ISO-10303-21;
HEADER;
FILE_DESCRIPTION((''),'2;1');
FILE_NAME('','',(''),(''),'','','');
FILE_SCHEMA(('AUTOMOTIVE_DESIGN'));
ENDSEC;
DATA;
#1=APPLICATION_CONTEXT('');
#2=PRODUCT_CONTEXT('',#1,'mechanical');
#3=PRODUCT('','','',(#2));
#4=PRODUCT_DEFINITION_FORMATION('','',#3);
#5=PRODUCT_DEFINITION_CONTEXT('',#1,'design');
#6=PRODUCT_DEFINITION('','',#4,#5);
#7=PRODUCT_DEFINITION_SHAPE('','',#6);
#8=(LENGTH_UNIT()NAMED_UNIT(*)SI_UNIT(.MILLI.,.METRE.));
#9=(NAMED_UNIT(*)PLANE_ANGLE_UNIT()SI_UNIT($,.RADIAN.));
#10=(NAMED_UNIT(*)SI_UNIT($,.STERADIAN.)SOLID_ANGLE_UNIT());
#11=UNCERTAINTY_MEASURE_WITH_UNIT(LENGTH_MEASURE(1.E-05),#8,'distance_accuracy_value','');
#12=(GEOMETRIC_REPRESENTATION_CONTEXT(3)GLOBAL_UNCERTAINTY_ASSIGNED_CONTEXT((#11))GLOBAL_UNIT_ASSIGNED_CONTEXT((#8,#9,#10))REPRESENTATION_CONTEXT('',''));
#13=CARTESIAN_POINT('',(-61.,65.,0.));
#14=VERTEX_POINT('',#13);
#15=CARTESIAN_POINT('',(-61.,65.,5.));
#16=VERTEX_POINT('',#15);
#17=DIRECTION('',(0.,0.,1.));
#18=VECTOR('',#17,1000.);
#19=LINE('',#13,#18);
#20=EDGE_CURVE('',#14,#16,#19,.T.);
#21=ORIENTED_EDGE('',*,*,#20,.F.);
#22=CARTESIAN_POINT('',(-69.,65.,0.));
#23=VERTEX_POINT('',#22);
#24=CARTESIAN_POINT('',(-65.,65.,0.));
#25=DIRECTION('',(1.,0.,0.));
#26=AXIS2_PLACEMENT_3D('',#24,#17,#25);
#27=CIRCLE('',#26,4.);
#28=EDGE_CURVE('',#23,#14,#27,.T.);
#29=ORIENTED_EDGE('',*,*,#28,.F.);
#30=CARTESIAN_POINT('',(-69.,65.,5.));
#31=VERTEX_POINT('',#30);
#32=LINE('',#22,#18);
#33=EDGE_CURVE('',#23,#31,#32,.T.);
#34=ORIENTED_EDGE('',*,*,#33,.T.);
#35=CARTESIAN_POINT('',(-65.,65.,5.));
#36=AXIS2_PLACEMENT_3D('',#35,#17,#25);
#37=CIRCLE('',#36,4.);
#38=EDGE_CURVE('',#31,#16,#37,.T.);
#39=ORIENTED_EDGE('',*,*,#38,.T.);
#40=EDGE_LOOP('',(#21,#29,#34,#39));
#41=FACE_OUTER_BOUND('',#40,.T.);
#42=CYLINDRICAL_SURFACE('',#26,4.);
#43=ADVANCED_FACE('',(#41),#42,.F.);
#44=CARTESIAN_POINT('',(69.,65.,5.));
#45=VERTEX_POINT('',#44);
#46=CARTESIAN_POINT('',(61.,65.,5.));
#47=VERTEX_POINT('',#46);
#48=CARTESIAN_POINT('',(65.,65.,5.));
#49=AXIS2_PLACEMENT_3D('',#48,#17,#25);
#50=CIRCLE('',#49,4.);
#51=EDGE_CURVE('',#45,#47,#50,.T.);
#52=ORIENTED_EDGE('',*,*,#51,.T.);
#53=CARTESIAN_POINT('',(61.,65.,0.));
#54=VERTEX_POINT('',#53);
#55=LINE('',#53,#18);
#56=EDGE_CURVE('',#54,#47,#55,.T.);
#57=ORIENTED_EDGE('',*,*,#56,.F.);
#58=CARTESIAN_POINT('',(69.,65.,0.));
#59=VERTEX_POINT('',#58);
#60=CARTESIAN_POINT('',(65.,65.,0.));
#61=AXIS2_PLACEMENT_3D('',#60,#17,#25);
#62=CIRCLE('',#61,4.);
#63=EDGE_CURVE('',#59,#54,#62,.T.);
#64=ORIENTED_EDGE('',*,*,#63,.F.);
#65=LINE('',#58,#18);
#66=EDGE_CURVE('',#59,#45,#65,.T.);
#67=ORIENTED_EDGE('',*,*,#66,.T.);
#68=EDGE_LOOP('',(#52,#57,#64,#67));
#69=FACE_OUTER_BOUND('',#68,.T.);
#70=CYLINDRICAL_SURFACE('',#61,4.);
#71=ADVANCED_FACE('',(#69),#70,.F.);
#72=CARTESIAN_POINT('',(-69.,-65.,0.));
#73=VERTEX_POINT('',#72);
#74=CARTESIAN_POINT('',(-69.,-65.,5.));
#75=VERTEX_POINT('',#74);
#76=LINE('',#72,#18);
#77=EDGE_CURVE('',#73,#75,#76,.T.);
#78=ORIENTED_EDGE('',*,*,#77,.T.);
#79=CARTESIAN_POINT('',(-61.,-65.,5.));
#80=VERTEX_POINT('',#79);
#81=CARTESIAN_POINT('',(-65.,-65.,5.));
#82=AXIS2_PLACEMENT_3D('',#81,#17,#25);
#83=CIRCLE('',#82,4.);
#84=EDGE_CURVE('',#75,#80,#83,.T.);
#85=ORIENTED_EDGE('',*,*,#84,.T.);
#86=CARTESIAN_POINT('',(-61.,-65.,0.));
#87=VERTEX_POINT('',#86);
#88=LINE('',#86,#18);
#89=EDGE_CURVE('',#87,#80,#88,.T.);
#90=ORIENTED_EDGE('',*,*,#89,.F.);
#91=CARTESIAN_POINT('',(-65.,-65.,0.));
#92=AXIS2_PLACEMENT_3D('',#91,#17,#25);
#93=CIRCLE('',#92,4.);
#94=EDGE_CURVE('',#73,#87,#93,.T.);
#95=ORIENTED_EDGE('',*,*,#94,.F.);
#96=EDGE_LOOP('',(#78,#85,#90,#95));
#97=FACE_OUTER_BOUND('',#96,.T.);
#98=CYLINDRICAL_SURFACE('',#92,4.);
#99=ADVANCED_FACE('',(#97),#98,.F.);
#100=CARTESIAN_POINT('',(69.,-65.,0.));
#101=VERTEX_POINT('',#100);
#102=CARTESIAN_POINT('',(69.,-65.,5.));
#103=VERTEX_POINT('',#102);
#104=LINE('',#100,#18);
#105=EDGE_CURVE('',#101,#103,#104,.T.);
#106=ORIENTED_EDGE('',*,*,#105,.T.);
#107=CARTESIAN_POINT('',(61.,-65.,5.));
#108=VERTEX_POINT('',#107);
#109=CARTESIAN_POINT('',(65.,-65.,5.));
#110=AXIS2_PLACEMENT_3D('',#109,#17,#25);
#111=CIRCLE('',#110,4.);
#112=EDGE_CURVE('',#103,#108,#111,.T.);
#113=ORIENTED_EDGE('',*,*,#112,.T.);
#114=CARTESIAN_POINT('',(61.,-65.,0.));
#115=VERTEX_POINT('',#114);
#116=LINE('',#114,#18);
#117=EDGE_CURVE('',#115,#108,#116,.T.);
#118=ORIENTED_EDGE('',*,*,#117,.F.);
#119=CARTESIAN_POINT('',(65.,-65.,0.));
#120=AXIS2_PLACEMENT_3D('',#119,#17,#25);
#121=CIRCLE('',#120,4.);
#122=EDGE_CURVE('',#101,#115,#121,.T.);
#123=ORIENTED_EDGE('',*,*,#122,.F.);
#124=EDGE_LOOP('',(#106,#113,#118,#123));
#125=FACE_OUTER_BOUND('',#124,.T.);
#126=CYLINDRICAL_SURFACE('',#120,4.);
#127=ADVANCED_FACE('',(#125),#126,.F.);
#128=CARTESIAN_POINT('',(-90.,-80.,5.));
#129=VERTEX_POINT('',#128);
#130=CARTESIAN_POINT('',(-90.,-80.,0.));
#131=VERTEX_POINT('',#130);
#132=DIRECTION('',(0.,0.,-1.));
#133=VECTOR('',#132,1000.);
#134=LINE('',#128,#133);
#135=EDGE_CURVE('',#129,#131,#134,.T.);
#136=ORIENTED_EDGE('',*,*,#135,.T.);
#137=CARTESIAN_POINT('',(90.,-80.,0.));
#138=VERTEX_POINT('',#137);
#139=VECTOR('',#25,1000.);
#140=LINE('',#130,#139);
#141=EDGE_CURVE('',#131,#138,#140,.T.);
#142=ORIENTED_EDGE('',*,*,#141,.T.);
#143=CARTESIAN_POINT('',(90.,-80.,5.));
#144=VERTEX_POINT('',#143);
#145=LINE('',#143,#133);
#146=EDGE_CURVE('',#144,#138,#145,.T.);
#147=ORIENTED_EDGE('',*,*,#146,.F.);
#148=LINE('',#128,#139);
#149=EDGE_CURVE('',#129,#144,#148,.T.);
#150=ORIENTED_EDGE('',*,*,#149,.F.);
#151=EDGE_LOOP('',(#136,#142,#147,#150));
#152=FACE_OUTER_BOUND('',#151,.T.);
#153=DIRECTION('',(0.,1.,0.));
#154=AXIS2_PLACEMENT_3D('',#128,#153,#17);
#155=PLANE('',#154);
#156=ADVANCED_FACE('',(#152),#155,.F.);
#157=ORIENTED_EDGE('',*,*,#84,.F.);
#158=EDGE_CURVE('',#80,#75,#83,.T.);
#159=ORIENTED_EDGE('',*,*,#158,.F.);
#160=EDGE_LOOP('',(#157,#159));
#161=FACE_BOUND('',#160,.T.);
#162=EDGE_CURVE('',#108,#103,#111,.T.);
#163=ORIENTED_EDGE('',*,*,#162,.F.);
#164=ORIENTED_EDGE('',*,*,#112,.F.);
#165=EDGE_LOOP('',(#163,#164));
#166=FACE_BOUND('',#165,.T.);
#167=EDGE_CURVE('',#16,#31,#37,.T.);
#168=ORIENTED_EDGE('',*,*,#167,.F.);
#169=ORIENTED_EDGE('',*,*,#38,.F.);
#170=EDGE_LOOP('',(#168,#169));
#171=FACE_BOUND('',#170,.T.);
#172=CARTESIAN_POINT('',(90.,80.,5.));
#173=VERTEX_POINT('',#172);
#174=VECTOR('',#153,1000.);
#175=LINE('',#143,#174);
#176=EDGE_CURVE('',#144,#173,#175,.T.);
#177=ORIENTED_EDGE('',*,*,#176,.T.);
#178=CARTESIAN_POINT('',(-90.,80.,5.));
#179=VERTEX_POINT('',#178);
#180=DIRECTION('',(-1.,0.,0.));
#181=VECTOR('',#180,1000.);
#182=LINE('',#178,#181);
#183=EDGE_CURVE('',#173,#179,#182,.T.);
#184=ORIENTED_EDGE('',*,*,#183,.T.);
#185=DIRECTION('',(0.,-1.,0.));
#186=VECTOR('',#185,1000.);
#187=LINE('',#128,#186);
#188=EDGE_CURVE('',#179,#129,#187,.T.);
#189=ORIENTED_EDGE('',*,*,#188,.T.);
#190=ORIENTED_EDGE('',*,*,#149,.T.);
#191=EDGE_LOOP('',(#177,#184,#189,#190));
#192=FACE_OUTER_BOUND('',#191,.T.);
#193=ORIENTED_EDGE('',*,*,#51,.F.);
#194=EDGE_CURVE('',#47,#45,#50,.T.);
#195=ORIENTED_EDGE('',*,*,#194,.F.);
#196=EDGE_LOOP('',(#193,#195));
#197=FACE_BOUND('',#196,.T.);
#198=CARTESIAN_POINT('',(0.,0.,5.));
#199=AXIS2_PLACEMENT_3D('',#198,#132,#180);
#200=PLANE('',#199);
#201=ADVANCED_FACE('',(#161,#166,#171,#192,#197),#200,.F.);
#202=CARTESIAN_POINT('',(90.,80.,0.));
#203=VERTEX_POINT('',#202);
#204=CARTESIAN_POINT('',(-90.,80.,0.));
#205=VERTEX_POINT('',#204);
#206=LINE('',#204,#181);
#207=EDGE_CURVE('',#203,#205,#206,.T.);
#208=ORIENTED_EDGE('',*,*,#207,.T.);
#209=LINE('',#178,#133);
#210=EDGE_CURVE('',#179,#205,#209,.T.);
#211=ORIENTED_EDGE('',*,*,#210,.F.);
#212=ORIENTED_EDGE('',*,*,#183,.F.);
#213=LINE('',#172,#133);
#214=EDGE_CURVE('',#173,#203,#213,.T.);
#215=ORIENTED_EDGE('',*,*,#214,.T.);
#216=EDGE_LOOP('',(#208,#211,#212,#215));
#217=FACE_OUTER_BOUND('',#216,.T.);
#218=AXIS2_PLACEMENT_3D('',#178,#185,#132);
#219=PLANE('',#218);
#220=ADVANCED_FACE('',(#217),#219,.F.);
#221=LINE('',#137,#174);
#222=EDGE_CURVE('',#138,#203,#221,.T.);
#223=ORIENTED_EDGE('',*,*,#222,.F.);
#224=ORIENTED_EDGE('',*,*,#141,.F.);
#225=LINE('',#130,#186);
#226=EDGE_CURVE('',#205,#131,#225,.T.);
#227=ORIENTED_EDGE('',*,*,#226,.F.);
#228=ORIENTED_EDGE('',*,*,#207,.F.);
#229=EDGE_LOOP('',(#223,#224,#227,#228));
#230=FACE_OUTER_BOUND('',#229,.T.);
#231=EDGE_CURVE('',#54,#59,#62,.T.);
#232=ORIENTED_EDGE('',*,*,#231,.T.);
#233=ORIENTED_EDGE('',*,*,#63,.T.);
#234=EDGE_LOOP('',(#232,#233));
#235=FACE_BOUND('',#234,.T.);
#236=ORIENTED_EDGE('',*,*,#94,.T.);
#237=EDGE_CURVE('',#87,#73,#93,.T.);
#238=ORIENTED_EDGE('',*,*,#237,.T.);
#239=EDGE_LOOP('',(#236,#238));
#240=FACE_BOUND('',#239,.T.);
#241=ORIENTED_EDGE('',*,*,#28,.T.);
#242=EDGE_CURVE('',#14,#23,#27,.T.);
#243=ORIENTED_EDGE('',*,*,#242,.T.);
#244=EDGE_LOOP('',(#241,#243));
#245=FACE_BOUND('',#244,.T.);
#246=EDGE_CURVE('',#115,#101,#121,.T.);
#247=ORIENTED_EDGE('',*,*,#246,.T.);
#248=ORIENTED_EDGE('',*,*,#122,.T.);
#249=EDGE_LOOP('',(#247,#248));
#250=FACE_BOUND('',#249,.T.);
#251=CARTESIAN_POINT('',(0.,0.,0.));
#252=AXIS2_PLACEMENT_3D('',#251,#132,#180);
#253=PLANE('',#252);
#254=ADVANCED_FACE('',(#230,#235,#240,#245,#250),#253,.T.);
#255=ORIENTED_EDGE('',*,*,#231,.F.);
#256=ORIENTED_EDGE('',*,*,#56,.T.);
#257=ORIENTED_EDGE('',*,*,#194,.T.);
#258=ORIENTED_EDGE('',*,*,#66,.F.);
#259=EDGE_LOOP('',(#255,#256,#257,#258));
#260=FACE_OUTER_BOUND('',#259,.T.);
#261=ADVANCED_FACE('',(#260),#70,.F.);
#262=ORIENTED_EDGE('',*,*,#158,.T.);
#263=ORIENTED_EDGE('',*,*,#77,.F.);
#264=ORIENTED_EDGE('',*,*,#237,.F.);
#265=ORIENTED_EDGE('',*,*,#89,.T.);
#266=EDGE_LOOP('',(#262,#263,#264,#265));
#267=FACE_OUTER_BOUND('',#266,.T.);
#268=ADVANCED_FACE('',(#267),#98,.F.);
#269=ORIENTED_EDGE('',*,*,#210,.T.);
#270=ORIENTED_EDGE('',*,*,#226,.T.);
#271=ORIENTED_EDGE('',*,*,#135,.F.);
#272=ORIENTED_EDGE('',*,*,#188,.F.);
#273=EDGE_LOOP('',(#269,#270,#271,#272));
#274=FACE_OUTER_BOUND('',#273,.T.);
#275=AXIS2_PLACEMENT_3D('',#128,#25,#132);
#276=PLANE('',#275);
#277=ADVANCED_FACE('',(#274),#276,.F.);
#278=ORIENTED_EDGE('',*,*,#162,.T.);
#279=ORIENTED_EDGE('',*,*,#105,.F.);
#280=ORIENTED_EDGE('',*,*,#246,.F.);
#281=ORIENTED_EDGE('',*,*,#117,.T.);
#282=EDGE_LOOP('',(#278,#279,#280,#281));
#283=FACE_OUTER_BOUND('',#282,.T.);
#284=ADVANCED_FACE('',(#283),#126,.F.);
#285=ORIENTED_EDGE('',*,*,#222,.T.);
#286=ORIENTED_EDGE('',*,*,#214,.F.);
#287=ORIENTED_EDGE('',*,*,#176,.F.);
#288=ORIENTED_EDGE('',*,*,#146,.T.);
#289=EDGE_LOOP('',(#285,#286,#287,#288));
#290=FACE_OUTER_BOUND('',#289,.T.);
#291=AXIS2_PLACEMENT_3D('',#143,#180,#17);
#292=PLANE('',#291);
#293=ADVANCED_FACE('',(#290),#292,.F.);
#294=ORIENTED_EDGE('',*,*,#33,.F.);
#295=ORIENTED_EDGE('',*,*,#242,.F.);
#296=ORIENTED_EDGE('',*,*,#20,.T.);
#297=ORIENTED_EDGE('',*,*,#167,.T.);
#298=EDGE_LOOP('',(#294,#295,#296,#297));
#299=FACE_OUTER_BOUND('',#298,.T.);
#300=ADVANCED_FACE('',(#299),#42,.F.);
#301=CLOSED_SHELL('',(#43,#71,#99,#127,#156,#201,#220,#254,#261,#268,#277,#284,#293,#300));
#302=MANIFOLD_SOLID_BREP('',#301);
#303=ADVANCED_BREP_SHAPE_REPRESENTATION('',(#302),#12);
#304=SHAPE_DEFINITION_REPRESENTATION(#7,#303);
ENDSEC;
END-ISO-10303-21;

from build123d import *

# Parameters (mm, degrees)
SKETCH_1_W          = 180
SKETCH_1_H          = 160
EXTRUDE_1_DEPTH     = 5
SKETCH_2_R          = 4
CUT_EXTRUDE_1_DEPTH = 121.519707932


with BuildPart() as part:
    # 草图1 → 凸台-拉伸1 (new body)
    with BuildSketch(Plane.XY):
        Rectangle(SKETCH_1_W, SKETCH_1_H)
    extrude(amount=EXTRUDE_1_DEPTH)

    # 草图2 → 切除-拉伸1 (cut, through all)
    with BuildSketch(Plane.XY.offset(5)):
        with Locations((-65, 65)):
            Circle(SKETCH_2_R)
        with Locations((65, 65)):
            Circle(SKETCH_2_R)
        with Locations((65, -65)):
            Circle(SKETCH_2_R)
        with Locations((-65, -65)):
            Circle(SKETCH_2_R)
    extrude(amount=-CUT_EXTRUDE_1_DEPTH, mode=Mode.SUBTRACT)


solid = part.part
